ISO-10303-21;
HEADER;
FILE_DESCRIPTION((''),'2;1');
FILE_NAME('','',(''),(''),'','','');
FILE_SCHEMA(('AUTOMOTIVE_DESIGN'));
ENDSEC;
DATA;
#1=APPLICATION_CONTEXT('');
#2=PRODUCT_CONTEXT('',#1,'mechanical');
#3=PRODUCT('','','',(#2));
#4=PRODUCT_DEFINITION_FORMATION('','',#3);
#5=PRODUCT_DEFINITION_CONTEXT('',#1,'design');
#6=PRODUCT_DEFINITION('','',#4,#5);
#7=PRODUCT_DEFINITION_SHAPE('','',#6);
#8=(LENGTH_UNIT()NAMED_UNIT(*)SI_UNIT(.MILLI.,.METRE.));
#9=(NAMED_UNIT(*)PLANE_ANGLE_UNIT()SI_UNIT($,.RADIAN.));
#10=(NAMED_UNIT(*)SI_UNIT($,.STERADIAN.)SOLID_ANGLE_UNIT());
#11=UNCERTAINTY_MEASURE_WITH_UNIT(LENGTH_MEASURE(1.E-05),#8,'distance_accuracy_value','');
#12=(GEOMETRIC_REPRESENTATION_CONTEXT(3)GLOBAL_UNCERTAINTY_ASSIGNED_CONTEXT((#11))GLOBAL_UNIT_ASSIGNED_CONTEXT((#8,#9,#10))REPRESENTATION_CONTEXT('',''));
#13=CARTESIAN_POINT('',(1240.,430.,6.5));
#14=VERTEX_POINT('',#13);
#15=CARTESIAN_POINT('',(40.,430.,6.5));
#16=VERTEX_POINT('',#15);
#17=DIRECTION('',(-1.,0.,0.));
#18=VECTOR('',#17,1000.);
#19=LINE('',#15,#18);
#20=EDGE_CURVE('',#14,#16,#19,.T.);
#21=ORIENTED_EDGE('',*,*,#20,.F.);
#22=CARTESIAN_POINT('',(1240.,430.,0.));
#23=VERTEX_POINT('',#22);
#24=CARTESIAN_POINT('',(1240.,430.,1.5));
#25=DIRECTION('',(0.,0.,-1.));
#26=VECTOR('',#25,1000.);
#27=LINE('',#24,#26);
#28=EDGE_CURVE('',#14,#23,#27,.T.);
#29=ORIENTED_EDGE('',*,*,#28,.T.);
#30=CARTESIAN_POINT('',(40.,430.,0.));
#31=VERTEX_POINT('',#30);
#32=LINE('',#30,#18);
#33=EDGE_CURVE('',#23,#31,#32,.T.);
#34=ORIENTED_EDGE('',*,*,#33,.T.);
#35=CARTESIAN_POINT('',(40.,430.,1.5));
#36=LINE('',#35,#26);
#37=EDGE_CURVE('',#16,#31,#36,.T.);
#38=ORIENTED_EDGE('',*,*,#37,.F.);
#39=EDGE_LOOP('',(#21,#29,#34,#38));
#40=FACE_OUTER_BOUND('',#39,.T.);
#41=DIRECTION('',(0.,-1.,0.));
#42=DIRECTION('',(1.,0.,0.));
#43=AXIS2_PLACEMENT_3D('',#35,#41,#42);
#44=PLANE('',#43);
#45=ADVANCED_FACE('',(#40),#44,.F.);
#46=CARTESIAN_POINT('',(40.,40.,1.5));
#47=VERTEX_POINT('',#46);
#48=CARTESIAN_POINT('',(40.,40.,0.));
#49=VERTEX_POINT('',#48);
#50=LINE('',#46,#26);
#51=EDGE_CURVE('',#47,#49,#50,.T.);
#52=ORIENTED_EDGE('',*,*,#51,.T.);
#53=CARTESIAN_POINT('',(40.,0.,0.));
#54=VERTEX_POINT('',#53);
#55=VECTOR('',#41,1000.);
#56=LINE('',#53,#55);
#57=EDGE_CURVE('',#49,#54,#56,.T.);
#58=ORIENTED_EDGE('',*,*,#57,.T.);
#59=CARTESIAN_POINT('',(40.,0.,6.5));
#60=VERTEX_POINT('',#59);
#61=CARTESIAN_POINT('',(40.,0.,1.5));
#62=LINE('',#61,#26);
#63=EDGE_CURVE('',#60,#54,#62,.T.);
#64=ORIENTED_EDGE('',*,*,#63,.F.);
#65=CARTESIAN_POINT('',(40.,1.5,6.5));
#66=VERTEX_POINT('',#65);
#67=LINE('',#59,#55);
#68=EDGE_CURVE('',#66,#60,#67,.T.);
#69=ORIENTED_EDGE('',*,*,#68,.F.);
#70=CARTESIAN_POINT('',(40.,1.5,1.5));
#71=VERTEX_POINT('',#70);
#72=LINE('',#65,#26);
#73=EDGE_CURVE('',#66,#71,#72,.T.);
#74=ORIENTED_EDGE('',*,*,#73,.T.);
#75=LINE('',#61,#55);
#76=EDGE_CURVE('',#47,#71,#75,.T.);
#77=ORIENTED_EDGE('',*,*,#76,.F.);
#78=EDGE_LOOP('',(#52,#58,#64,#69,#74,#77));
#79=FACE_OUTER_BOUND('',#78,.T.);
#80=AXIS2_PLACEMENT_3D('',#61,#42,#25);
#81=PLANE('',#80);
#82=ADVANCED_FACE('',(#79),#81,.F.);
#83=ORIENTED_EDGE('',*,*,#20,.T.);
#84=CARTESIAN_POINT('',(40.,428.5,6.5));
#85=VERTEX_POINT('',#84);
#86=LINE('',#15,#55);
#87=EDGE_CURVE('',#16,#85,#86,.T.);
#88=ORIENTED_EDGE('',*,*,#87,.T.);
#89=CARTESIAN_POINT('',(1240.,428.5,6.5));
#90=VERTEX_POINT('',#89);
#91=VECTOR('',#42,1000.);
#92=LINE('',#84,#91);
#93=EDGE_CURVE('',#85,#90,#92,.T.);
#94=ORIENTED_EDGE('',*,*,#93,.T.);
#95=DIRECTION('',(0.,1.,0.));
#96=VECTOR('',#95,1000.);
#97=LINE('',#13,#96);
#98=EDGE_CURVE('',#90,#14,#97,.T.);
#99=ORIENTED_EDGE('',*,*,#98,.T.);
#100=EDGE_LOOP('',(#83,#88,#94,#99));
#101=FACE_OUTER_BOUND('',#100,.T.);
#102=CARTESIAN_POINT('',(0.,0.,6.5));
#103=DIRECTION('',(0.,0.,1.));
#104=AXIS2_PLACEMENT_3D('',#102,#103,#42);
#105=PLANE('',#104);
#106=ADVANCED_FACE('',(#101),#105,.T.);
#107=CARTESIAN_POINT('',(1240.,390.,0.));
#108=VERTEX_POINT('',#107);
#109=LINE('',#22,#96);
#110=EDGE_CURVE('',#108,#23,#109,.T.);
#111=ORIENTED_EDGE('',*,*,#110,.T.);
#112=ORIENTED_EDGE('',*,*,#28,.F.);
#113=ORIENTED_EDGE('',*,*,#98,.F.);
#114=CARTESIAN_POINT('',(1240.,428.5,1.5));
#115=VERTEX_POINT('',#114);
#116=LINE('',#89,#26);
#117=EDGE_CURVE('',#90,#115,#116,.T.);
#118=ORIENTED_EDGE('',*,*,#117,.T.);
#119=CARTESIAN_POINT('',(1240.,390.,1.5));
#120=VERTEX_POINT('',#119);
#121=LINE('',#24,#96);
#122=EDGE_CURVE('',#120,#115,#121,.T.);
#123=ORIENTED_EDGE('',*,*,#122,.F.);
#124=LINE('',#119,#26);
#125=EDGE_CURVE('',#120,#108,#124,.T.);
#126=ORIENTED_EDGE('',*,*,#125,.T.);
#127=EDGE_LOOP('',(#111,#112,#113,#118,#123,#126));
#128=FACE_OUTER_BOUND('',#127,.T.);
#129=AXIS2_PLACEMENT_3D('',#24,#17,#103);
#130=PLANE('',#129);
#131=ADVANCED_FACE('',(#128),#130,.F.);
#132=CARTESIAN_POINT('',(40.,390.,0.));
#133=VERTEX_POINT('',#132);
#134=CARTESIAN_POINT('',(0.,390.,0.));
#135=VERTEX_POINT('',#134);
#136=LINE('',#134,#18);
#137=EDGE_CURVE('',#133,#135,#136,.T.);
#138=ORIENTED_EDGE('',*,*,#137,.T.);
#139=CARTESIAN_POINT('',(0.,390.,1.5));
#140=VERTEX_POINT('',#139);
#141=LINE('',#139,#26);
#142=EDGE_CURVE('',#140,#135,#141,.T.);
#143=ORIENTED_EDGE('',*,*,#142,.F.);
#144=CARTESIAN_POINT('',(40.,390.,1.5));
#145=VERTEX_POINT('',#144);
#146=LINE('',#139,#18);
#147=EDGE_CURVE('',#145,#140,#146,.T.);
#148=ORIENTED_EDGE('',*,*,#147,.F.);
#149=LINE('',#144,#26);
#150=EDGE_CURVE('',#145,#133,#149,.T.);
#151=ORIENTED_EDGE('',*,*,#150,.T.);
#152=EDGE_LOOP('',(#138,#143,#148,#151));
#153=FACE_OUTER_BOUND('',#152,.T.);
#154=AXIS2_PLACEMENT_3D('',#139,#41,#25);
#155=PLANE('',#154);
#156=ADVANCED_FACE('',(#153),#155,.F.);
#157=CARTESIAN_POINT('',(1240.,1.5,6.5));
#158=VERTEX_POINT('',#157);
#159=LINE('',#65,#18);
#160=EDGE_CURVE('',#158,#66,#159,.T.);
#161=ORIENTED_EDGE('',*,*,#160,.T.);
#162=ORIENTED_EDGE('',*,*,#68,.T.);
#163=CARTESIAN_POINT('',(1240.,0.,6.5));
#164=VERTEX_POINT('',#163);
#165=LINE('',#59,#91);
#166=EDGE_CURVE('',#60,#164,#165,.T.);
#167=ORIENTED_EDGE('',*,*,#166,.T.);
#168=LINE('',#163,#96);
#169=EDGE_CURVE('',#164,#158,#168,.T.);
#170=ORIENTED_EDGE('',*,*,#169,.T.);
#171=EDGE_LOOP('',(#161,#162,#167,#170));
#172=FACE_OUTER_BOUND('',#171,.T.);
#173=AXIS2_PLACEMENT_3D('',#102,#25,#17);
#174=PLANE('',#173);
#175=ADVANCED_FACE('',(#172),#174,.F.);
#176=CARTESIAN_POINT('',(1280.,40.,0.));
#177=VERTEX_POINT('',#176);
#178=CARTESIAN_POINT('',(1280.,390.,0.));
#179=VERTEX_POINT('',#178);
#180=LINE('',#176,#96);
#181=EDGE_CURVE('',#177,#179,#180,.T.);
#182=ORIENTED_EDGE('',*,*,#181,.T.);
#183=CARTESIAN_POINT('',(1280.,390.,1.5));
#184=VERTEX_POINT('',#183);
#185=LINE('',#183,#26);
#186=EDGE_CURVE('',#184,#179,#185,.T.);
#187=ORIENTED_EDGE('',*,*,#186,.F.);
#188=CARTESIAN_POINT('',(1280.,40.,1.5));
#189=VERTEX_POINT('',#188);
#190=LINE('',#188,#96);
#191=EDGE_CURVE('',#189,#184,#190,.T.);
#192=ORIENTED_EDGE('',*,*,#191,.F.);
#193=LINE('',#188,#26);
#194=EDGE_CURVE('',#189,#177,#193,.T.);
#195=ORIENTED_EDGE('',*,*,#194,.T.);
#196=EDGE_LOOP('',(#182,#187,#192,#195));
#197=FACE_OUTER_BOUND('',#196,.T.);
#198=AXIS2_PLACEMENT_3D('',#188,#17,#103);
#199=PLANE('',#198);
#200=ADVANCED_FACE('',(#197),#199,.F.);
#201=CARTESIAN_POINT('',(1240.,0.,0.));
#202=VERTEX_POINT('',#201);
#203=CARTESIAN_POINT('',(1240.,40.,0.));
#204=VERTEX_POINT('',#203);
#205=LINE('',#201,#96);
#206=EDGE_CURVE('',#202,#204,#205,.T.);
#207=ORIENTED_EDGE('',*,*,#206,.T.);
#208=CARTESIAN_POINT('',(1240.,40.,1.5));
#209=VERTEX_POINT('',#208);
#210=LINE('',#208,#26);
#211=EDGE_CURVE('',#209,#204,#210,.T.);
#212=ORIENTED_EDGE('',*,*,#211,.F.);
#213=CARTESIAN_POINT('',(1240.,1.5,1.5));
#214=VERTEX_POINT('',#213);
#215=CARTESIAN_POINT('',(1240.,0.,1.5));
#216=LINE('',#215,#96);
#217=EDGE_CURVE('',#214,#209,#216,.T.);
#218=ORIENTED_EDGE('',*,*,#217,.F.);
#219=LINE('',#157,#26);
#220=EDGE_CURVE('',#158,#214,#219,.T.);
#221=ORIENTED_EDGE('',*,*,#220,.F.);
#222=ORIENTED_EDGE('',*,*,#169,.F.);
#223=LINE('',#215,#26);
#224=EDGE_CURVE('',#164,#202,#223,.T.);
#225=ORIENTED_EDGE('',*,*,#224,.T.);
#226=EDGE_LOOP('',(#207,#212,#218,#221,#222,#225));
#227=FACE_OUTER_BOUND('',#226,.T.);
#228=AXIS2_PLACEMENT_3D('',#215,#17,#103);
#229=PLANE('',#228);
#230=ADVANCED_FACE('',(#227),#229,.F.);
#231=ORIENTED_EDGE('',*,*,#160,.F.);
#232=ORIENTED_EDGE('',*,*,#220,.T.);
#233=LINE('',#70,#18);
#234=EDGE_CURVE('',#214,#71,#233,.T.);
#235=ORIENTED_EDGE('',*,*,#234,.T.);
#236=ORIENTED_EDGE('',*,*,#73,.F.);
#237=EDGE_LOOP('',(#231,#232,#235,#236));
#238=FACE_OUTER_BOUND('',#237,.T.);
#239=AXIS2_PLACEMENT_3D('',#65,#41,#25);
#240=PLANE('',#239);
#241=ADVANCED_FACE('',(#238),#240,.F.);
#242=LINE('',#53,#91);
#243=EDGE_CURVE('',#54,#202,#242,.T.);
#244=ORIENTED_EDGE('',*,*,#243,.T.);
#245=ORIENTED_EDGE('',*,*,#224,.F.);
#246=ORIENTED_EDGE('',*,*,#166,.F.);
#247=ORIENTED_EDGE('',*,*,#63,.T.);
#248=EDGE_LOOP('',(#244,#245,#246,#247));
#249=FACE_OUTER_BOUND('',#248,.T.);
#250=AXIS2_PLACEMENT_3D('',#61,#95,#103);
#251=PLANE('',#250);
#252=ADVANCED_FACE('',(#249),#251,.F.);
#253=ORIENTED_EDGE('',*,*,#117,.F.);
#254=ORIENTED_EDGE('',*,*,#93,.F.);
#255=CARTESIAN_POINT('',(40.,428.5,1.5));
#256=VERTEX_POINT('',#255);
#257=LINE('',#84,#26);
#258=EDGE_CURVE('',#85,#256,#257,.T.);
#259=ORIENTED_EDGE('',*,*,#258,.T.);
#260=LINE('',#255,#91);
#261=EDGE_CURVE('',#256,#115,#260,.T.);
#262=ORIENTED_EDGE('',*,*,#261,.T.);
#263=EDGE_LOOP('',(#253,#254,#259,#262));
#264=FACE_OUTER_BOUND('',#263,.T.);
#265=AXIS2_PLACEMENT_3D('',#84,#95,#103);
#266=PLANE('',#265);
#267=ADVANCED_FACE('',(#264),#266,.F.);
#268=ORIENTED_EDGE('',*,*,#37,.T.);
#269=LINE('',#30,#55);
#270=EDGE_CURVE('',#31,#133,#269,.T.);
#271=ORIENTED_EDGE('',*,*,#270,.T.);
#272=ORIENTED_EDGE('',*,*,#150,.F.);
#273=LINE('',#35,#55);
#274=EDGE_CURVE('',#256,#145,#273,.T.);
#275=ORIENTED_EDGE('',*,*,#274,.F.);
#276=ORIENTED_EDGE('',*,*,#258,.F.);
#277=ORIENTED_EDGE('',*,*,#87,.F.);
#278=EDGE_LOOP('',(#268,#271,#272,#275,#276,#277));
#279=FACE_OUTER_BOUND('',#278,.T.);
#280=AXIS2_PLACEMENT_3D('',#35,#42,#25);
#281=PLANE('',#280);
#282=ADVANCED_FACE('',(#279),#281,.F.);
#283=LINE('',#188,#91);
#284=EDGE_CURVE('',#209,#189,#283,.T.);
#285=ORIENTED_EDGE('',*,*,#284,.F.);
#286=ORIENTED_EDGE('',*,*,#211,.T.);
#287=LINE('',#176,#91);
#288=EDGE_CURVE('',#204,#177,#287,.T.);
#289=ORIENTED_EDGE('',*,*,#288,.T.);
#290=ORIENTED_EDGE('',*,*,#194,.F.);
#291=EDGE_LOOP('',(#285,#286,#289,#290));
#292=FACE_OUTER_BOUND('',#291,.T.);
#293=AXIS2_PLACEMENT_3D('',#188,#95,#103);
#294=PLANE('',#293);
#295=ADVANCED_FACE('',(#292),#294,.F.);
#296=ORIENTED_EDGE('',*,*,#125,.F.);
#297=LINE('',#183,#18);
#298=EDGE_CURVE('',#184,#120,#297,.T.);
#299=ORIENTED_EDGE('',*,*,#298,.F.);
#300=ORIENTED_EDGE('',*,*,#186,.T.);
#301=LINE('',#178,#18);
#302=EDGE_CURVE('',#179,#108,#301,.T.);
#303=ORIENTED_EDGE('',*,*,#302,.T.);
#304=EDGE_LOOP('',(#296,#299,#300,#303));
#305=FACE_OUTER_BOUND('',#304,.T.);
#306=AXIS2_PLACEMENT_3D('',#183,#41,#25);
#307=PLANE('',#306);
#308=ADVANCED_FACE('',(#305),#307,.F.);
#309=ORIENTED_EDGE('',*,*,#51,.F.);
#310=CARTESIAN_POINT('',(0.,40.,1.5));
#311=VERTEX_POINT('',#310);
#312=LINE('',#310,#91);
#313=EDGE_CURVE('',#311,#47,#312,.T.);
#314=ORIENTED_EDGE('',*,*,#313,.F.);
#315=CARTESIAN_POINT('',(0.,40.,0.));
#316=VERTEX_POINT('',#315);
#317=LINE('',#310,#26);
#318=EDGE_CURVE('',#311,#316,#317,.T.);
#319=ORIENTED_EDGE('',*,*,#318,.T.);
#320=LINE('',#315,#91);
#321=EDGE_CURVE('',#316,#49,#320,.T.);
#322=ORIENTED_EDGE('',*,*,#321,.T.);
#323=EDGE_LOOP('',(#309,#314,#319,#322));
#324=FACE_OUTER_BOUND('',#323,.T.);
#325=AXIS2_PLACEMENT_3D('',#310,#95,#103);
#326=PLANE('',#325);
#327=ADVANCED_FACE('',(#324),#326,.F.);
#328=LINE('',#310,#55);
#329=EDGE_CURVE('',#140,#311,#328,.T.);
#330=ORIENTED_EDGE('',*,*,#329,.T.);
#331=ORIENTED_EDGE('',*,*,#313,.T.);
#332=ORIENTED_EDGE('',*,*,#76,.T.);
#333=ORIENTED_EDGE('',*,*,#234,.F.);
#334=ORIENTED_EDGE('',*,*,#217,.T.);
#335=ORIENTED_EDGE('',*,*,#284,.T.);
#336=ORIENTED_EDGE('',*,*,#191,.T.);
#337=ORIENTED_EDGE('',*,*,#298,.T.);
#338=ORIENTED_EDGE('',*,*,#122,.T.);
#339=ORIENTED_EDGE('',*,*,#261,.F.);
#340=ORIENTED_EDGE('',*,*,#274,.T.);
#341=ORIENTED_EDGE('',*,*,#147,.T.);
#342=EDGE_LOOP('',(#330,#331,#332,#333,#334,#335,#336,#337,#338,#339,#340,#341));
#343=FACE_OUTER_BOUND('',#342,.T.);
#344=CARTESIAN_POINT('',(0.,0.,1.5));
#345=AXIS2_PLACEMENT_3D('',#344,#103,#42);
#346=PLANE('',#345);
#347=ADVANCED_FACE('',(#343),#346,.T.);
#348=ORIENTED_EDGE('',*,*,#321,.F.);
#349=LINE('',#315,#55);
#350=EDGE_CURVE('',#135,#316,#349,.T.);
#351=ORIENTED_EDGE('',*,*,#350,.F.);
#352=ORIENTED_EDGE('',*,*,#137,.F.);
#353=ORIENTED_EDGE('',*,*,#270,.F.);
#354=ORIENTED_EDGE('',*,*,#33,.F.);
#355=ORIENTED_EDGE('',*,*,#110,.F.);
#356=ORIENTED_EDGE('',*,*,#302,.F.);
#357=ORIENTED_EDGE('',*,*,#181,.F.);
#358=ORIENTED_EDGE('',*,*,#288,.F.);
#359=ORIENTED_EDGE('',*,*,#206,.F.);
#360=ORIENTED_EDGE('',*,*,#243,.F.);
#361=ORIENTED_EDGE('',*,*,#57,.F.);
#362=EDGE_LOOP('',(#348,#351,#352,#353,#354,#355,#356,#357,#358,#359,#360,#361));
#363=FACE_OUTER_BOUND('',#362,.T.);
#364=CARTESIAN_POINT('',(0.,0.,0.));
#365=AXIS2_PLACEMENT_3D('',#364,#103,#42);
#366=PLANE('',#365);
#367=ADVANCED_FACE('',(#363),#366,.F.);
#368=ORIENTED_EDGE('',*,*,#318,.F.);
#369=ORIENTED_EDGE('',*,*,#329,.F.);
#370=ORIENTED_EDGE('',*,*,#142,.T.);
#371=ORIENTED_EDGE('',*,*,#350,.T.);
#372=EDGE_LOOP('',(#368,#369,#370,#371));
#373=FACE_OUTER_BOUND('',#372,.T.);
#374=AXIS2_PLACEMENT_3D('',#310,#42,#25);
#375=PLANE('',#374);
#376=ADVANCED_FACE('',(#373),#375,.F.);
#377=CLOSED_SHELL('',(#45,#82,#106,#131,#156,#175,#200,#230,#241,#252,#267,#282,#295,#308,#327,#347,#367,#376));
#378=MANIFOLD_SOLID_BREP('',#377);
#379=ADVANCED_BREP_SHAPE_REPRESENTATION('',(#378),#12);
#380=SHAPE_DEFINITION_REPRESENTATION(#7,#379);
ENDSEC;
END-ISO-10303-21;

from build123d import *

# Parameters (mm, degrees)
BOSS_EXTRUDE1_DEPTH = 1.5
SKETCH2_W           = 1200
SKETCH2_H           = 1.5
BOSS_EXTRUDE2_DEPTH = 5


with BuildPart() as part:
    # Sketch1 → Boss-Extrude1 (new body)
    with BuildSketch(Plane.XY):
        Polygon((40, 0), (1240, 0), (1240, 40), (1280, 40), (1280, 390), (1240, 390), (1240, 430), (40, 430), (40, 390), (0, 390), (0, 40), (40, 40), align=None)
    extrude(amount=BOSS_EXTRUDE1_DEPTH)

    # Sketch2 → Boss-Extrude2 (add)
    with BuildSketch(Plane.XY.offset(1.5)):
        with Locations((640, 429.25)):
            Rectangle(SKETCH2_W, SKETCH2_H)
        with Locations((640, 0.75)):
            Rectangle(SKETCH2_W, SKETCH2_H)
    extrude(amount=BOSS_EXTRUDE2_DEPTH)


solid = part.part
